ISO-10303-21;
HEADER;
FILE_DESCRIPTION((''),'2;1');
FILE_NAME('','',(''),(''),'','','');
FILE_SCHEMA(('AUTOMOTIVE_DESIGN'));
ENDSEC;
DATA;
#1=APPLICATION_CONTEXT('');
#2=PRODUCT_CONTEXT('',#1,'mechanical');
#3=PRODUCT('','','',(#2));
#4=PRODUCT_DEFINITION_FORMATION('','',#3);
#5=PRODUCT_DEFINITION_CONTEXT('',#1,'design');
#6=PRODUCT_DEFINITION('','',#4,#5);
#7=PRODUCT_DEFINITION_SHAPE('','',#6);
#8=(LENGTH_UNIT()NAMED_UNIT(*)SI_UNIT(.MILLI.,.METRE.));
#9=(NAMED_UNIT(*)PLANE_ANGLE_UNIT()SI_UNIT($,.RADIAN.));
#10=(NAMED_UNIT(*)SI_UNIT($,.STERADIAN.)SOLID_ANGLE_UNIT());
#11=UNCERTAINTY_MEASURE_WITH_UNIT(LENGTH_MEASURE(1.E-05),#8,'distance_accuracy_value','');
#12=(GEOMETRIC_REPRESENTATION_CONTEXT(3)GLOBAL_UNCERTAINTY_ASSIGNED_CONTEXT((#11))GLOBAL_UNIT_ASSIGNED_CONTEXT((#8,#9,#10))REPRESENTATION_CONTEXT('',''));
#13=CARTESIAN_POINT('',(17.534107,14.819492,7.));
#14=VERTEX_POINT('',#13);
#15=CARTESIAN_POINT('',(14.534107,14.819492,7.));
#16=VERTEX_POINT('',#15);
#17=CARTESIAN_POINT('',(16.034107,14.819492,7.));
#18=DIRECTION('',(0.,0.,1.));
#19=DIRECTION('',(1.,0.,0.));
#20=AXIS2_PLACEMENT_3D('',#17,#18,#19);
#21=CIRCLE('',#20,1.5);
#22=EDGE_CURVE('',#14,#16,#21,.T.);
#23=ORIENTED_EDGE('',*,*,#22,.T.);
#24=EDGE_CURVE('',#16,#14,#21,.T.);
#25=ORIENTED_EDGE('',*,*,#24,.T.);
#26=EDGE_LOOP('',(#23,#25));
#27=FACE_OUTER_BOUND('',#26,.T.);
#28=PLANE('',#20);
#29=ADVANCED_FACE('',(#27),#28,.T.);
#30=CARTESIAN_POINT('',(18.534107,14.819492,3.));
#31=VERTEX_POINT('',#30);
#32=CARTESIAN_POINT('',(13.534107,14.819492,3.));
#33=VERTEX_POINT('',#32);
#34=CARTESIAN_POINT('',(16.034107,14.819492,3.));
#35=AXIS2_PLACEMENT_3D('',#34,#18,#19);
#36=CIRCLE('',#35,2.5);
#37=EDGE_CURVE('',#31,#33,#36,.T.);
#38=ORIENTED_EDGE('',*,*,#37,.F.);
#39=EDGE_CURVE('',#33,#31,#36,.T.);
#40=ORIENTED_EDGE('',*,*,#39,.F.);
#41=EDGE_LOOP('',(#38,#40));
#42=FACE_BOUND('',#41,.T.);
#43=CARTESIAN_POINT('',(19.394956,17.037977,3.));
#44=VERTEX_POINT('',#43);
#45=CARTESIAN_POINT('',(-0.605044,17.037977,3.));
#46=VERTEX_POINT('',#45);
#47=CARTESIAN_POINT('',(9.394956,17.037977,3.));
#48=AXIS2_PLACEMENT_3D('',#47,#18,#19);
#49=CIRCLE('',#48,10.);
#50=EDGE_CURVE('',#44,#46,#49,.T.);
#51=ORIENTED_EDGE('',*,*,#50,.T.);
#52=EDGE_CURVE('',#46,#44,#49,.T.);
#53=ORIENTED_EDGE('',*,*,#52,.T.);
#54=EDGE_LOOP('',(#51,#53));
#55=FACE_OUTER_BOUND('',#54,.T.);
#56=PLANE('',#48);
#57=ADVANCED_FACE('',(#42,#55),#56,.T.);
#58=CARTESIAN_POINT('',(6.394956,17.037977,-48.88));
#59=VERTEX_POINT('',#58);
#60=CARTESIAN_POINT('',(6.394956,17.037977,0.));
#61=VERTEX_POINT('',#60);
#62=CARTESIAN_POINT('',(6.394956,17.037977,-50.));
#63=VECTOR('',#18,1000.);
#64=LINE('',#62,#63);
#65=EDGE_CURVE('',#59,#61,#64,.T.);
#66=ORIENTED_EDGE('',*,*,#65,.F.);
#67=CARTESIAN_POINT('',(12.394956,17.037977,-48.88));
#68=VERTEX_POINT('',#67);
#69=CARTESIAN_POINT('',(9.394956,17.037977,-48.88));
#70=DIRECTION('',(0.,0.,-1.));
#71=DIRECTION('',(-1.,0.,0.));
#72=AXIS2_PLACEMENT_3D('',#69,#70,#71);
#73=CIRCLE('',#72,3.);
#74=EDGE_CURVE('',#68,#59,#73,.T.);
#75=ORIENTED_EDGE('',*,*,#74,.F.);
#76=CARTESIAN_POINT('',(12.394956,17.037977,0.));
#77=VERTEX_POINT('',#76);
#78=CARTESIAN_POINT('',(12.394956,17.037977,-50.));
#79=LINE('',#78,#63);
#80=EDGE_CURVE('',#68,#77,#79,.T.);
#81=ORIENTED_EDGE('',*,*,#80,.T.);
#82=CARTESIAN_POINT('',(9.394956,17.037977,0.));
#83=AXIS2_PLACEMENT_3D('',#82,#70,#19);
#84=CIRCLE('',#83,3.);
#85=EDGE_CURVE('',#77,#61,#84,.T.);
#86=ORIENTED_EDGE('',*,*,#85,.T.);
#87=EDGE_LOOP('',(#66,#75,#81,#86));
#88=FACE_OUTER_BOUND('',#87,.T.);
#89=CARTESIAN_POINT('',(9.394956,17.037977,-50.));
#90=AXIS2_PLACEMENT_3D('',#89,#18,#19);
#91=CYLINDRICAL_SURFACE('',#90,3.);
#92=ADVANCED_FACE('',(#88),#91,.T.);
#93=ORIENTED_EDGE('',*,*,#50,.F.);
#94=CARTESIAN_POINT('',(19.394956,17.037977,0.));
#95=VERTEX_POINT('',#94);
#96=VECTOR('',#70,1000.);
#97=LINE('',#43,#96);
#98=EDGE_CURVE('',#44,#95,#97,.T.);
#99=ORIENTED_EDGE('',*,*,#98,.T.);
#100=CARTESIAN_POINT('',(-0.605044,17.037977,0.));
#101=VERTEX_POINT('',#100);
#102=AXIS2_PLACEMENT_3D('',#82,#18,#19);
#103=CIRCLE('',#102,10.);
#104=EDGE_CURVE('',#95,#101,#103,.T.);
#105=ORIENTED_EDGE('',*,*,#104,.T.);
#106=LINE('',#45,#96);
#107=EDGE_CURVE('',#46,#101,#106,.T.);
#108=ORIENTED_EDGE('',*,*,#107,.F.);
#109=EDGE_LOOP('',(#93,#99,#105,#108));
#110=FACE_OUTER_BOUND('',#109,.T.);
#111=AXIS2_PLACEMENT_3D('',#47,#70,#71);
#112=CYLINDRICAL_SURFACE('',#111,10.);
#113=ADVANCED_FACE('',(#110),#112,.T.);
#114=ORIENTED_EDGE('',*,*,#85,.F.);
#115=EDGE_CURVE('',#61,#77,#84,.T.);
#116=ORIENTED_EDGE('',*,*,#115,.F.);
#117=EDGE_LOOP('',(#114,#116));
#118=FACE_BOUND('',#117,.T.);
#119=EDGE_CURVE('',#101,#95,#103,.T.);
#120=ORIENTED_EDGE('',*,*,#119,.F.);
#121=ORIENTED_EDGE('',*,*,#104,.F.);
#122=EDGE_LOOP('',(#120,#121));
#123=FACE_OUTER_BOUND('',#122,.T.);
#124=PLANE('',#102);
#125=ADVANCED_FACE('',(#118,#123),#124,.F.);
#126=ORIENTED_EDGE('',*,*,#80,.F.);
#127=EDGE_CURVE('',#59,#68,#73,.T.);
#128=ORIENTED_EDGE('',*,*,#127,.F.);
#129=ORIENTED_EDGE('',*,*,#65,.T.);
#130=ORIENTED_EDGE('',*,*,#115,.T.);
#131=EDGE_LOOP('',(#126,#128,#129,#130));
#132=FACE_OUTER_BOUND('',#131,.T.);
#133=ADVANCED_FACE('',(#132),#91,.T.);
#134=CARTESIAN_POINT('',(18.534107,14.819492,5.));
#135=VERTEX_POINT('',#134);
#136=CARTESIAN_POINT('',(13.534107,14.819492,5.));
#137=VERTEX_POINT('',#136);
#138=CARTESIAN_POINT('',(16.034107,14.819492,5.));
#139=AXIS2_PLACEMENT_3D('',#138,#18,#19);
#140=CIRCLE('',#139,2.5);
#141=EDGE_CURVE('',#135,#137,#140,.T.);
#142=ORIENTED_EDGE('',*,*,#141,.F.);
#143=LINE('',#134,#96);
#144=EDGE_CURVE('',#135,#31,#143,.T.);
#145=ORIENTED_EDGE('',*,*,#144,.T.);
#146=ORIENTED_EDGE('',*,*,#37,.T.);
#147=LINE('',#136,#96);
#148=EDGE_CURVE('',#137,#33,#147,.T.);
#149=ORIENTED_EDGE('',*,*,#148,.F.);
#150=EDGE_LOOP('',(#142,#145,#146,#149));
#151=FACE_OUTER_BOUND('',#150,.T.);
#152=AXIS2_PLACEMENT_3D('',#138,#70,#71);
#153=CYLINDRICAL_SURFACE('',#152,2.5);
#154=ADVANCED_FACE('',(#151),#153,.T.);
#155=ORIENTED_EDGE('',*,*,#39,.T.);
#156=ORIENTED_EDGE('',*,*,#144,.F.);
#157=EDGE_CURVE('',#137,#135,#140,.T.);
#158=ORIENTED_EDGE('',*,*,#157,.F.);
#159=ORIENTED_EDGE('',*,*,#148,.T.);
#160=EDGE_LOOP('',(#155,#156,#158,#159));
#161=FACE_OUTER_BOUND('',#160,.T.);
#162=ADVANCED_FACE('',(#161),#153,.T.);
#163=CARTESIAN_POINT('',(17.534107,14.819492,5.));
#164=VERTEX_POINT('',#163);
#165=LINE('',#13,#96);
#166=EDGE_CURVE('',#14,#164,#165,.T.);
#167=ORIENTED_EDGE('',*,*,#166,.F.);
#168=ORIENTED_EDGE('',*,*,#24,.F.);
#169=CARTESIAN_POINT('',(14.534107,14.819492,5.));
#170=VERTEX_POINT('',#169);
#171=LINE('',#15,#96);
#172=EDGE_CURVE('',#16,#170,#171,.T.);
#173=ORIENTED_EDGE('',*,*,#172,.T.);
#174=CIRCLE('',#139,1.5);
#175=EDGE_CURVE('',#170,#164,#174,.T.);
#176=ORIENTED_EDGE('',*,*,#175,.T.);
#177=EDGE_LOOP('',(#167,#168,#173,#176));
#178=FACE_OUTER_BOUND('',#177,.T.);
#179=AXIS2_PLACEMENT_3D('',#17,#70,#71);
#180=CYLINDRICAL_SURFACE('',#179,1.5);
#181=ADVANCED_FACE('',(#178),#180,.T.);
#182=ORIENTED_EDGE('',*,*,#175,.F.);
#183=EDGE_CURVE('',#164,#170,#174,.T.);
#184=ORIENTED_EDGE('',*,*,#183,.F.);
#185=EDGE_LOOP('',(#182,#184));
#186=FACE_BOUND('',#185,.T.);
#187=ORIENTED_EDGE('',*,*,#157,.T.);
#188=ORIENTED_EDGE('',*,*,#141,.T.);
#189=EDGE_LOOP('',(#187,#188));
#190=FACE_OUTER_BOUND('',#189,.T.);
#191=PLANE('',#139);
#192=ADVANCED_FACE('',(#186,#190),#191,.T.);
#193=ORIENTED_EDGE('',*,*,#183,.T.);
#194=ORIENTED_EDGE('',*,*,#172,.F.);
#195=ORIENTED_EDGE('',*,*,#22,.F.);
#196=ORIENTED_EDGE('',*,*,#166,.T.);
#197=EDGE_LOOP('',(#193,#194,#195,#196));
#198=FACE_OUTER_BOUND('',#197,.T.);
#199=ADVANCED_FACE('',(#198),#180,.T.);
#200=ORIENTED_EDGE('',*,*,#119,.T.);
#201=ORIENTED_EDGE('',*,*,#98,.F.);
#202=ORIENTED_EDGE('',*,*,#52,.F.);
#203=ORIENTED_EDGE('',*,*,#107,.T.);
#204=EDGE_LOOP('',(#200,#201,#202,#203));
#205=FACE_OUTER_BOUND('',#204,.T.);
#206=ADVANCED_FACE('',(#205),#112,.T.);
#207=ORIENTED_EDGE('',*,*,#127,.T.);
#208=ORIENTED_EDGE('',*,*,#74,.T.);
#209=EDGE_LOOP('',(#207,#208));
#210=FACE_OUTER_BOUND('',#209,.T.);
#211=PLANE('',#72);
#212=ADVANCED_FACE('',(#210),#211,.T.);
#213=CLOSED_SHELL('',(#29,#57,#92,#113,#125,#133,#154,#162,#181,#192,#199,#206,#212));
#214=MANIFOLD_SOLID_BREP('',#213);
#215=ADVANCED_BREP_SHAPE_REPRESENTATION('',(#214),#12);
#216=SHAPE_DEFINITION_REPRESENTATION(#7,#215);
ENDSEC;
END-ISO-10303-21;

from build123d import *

# Parameters (mm, degrees)
SKETCH1_R           = 10
BOSS_EXTRUDE1_DEPTH = 3
SKETCH2_R           = 2.5
BOSS_EXTRUDE2_DEPTH = 2
SKETCH3_R           = 1.5
BOSS_EXTRUDE3_DEPTH = 2
SKETCH4_R           = 3
BOSS_EXTRUDE4_DEPTH = 50
CUT_EXTRUDE1_START  = -2.12
SKETCH5_R           = 3
CUT_EXTRUDE1_DEPTH  = 2.12
SKETCH6_R           = 3
BOSS_EXTRUDE5_DEPTH = 1


with BuildPart() as part:
    # Sketch1 → Boss-Extrude1 (new body)
    with BuildSketch(Plane.XY):
        with Locations((9.394956339, 17.03797738)):
            Circle(SKETCH1_R)
    extrude(amount=BOSS_EXTRUDE1_DEPTH)

    # Sketch2 → Boss-Extrude2 (add)
    with BuildSketch(Plane.XY.offset(3)):
        with Locations((16.034106962, 14.819491633)):
            Circle(SKETCH2_R)
    extrude(amount=BOSS_EXTRUDE2_DEPTH)

    # Sketch3 → Boss-Extrude3 (add)
    with BuildSketch(Plane.XY.offset(5)):
        with Locations((16.034106962, 14.819491633)):
            Circle(SKETCH3_R)
    extrude(amount=BOSS_EXTRUDE3_DEPTH)

    # Sketch4 → Boss-Extrude4 (add)
    with BuildSketch(Plane(origin=(0, 0, 0), x_dir=(-1, 0, 0), z_dir=(0, 0, -1))):
        with Locations(Location((-9.394956339, 17.03797738, 0), (0, 0, 180))):
            Circle(SKETCH4_R)
    extrude(amount=BOSS_EXTRUDE4_DEPTH)

    # Sketch5 → Cut-Extrude1 (cut)
    with BuildSketch(Plane(origin=(0, 0, -50), x_dir=(-1, 0, 0), z_dir=(0, 0, -1)).offset(CUT_EXTRUDE1_START)):
        with Locations(Location((-9.394956339, 17.03797738, 0), (0, 0, 180))):
            Circle(SKETCH5_R)
    extrude(amount=CUT_EXTRUDE1_DEPTH, mode=Mode.SUBTRACT)

    # Sketch6 → Boss-Extrude5 (add)
    with BuildSketch(Plane(origin=(0, 0, -47.88), x_dir=(-1, 0, 0), z_dir=(0, 0, -1))):
        with Locations(Location((-9.394956339, 17.03797738, 0), (0, 0, 180))):
            Circle(SKETCH6_R)
    extrude(amount=BOSS_EXTRUDE5_DEPTH)


solid = part.part
